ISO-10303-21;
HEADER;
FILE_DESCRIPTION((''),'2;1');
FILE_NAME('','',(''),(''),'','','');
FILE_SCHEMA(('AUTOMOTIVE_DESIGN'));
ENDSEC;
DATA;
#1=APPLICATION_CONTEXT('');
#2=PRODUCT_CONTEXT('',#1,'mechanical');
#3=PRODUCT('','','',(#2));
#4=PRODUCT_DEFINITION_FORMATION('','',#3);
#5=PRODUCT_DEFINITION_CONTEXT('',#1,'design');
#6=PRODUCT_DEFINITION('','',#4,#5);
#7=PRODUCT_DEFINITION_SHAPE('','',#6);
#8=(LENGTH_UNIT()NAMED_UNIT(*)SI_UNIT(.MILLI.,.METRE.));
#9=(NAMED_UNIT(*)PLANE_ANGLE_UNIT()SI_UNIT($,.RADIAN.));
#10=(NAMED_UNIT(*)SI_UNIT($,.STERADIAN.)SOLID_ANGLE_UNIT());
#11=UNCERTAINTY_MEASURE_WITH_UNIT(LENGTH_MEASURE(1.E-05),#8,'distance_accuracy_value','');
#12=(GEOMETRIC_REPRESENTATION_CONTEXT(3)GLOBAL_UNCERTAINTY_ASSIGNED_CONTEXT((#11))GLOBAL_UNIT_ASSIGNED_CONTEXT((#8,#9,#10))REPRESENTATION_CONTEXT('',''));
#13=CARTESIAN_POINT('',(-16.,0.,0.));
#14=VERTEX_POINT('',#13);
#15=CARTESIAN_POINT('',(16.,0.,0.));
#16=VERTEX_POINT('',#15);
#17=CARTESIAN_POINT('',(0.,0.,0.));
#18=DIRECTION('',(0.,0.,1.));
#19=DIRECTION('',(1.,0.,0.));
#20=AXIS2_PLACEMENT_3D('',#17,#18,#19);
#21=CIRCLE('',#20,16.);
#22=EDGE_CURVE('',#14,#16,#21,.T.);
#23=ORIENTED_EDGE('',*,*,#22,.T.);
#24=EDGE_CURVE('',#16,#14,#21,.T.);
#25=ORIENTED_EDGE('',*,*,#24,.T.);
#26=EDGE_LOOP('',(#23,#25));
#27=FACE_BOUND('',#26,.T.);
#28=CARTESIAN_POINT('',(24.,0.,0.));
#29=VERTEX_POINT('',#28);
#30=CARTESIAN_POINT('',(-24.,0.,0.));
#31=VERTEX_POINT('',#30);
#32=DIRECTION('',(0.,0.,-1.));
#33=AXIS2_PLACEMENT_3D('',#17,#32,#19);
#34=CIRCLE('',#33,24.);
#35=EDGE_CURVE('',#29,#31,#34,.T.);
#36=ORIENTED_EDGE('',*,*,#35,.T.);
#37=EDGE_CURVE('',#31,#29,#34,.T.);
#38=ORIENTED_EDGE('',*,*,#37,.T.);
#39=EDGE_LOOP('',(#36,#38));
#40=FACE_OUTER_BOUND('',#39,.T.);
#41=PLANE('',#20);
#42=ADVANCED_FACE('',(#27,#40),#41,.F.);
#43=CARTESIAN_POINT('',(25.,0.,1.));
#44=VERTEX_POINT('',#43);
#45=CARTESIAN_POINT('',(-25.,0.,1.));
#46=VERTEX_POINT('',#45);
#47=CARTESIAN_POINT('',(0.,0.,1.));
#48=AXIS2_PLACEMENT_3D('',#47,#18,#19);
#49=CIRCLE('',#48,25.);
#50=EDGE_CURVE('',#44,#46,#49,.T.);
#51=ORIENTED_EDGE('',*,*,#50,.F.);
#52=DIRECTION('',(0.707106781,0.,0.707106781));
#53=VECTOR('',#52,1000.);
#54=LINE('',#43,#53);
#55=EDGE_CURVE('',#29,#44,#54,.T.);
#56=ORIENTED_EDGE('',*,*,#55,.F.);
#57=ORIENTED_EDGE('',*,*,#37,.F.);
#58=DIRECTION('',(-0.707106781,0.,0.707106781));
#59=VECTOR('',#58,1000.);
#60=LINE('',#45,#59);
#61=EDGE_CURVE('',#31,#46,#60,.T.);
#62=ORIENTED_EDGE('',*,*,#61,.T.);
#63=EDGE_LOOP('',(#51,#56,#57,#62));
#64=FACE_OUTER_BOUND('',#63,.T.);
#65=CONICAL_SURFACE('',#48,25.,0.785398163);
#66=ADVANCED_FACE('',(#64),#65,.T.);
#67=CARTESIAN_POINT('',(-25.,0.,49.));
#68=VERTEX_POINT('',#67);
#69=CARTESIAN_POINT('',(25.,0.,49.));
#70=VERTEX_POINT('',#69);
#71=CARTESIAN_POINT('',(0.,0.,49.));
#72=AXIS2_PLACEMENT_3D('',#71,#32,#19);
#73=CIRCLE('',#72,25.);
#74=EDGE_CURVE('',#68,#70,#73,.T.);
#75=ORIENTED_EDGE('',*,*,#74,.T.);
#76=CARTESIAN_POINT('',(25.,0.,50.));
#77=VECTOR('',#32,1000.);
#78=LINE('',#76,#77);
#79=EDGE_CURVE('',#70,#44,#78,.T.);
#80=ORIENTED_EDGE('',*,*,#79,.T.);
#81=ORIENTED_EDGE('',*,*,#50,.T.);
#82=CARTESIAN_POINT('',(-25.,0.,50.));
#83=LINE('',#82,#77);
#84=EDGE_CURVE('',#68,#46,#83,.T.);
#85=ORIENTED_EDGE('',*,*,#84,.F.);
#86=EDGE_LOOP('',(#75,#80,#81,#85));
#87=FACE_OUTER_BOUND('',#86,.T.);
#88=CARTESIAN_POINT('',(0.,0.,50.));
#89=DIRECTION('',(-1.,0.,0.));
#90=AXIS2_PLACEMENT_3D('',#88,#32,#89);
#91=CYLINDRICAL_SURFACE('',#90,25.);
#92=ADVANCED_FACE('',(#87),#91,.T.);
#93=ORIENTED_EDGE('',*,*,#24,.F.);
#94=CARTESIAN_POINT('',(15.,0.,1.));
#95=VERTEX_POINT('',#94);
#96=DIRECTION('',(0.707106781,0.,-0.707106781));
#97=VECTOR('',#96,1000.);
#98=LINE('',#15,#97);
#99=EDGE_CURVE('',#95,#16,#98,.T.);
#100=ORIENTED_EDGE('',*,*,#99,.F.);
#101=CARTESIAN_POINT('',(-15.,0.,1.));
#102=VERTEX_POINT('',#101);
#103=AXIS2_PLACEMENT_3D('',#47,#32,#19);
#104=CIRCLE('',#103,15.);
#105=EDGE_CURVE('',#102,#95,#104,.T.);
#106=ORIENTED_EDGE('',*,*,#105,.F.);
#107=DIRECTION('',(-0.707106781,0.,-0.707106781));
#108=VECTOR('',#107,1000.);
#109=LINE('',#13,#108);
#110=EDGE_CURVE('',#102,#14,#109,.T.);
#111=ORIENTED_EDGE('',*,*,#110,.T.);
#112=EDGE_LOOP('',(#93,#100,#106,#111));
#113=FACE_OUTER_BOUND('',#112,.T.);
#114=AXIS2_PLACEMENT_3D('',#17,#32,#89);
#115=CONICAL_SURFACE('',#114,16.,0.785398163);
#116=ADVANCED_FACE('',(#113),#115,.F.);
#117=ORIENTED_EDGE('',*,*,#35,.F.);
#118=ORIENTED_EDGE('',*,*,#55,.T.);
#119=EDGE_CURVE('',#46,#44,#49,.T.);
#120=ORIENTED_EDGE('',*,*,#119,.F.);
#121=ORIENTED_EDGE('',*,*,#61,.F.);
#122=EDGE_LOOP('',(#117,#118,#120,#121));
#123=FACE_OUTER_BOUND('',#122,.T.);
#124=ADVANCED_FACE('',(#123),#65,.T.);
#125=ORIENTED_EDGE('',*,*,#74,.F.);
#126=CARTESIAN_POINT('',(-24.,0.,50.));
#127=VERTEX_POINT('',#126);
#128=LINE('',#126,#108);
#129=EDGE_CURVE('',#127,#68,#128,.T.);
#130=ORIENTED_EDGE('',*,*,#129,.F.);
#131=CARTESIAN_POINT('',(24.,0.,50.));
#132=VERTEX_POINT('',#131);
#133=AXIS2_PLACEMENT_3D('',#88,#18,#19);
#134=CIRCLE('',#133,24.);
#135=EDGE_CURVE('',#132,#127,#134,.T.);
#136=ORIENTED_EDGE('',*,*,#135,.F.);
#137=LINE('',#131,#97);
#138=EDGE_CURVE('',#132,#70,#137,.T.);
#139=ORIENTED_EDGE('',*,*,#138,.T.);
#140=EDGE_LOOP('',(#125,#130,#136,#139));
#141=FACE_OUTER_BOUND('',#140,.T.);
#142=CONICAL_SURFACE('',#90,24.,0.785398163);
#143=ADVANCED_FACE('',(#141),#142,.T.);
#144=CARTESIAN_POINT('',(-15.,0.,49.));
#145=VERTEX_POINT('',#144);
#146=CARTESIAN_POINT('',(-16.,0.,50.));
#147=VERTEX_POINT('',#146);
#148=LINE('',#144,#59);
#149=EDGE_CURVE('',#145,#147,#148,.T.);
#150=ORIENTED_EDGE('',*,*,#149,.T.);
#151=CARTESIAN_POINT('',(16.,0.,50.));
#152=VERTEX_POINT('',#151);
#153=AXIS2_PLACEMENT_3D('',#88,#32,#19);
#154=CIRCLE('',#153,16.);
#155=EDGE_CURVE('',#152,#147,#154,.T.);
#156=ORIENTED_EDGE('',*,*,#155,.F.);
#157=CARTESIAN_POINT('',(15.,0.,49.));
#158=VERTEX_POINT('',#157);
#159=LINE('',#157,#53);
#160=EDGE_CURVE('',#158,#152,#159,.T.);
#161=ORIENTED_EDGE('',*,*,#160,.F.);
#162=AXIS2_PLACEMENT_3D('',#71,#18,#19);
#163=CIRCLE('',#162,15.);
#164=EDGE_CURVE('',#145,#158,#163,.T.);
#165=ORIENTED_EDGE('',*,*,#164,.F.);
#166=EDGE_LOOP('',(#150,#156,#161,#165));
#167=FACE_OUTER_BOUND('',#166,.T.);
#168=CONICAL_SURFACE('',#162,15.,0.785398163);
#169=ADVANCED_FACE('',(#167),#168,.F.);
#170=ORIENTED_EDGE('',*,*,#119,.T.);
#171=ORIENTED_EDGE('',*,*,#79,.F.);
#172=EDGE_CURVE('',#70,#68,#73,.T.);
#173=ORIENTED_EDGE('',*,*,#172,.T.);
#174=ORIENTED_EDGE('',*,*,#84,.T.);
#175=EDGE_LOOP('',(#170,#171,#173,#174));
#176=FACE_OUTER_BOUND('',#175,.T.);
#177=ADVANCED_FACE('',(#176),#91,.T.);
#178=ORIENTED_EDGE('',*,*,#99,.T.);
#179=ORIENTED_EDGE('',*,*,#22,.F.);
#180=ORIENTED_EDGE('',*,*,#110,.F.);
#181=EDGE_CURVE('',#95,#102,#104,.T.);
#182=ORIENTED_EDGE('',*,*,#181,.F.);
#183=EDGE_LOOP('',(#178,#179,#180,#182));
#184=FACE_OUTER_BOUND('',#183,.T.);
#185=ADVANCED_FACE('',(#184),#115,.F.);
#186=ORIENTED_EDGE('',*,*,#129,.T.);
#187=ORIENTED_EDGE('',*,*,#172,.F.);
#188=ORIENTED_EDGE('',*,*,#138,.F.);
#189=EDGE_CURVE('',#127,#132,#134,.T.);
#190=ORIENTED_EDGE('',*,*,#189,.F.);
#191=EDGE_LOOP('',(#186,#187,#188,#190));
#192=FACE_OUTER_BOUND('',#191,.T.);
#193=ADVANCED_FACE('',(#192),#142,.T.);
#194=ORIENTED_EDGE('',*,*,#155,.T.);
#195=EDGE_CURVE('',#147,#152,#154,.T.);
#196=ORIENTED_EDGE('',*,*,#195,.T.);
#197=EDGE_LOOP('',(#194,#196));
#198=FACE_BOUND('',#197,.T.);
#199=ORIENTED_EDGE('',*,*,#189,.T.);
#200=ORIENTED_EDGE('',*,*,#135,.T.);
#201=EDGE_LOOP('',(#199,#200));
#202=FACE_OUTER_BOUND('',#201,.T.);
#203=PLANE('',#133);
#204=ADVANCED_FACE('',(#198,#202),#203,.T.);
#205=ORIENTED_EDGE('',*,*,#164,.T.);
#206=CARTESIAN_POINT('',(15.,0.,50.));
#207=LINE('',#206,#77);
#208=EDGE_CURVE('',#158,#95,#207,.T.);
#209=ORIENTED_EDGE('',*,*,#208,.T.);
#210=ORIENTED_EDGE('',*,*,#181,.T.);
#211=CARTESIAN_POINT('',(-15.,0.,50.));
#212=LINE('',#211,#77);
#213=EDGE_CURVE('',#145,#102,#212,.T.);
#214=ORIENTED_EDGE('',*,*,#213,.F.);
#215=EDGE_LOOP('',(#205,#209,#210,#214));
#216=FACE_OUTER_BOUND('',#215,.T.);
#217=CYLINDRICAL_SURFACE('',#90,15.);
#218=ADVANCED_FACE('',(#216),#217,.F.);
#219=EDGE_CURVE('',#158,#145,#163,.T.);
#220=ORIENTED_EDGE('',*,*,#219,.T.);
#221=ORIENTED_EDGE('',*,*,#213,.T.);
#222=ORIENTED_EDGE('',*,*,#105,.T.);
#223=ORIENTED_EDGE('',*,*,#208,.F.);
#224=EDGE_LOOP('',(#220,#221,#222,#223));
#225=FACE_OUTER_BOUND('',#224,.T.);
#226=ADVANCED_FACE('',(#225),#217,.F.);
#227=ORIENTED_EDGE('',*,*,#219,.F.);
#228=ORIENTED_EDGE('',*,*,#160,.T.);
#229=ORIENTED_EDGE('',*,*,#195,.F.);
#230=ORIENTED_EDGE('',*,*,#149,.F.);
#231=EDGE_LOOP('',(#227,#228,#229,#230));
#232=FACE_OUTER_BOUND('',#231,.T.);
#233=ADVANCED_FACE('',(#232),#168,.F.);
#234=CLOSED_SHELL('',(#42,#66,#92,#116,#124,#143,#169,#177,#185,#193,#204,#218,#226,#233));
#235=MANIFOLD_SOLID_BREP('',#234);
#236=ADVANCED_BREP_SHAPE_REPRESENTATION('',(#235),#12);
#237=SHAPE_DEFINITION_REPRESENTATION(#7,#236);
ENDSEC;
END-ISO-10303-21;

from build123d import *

# Parameters (mm, degrees)
SKETCH1_R           = 25
SKETCH1_R_2         = 15
BOSS_EXTRUDE1_DEPTH = 50
CHAMFER1_SIZE       = 1


with BuildPart() as part:
    # Sketch1 → Boss-Extrude1 (new body)
    with BuildSketch(Plane.XY):
        Circle(SKETCH1_R)
        Circle(SKETCH1_R_2, mode=Mode.SUBTRACT)
    extrude(amount=BOSS_EXTRUDE1_DEPTH)

    # Chamfer1
    chamfer1_edges = [part.edges().sort_by_distance(p)[0] for p in [
        (-25, 0, 0),
        (-25, 0, 50),
        (-15, 0, 0),
        (-15, 0, 50),
    ]]
    chamfer(chamfer1_edges, length=CHAMFER1_SIZE)


solid = part.part
